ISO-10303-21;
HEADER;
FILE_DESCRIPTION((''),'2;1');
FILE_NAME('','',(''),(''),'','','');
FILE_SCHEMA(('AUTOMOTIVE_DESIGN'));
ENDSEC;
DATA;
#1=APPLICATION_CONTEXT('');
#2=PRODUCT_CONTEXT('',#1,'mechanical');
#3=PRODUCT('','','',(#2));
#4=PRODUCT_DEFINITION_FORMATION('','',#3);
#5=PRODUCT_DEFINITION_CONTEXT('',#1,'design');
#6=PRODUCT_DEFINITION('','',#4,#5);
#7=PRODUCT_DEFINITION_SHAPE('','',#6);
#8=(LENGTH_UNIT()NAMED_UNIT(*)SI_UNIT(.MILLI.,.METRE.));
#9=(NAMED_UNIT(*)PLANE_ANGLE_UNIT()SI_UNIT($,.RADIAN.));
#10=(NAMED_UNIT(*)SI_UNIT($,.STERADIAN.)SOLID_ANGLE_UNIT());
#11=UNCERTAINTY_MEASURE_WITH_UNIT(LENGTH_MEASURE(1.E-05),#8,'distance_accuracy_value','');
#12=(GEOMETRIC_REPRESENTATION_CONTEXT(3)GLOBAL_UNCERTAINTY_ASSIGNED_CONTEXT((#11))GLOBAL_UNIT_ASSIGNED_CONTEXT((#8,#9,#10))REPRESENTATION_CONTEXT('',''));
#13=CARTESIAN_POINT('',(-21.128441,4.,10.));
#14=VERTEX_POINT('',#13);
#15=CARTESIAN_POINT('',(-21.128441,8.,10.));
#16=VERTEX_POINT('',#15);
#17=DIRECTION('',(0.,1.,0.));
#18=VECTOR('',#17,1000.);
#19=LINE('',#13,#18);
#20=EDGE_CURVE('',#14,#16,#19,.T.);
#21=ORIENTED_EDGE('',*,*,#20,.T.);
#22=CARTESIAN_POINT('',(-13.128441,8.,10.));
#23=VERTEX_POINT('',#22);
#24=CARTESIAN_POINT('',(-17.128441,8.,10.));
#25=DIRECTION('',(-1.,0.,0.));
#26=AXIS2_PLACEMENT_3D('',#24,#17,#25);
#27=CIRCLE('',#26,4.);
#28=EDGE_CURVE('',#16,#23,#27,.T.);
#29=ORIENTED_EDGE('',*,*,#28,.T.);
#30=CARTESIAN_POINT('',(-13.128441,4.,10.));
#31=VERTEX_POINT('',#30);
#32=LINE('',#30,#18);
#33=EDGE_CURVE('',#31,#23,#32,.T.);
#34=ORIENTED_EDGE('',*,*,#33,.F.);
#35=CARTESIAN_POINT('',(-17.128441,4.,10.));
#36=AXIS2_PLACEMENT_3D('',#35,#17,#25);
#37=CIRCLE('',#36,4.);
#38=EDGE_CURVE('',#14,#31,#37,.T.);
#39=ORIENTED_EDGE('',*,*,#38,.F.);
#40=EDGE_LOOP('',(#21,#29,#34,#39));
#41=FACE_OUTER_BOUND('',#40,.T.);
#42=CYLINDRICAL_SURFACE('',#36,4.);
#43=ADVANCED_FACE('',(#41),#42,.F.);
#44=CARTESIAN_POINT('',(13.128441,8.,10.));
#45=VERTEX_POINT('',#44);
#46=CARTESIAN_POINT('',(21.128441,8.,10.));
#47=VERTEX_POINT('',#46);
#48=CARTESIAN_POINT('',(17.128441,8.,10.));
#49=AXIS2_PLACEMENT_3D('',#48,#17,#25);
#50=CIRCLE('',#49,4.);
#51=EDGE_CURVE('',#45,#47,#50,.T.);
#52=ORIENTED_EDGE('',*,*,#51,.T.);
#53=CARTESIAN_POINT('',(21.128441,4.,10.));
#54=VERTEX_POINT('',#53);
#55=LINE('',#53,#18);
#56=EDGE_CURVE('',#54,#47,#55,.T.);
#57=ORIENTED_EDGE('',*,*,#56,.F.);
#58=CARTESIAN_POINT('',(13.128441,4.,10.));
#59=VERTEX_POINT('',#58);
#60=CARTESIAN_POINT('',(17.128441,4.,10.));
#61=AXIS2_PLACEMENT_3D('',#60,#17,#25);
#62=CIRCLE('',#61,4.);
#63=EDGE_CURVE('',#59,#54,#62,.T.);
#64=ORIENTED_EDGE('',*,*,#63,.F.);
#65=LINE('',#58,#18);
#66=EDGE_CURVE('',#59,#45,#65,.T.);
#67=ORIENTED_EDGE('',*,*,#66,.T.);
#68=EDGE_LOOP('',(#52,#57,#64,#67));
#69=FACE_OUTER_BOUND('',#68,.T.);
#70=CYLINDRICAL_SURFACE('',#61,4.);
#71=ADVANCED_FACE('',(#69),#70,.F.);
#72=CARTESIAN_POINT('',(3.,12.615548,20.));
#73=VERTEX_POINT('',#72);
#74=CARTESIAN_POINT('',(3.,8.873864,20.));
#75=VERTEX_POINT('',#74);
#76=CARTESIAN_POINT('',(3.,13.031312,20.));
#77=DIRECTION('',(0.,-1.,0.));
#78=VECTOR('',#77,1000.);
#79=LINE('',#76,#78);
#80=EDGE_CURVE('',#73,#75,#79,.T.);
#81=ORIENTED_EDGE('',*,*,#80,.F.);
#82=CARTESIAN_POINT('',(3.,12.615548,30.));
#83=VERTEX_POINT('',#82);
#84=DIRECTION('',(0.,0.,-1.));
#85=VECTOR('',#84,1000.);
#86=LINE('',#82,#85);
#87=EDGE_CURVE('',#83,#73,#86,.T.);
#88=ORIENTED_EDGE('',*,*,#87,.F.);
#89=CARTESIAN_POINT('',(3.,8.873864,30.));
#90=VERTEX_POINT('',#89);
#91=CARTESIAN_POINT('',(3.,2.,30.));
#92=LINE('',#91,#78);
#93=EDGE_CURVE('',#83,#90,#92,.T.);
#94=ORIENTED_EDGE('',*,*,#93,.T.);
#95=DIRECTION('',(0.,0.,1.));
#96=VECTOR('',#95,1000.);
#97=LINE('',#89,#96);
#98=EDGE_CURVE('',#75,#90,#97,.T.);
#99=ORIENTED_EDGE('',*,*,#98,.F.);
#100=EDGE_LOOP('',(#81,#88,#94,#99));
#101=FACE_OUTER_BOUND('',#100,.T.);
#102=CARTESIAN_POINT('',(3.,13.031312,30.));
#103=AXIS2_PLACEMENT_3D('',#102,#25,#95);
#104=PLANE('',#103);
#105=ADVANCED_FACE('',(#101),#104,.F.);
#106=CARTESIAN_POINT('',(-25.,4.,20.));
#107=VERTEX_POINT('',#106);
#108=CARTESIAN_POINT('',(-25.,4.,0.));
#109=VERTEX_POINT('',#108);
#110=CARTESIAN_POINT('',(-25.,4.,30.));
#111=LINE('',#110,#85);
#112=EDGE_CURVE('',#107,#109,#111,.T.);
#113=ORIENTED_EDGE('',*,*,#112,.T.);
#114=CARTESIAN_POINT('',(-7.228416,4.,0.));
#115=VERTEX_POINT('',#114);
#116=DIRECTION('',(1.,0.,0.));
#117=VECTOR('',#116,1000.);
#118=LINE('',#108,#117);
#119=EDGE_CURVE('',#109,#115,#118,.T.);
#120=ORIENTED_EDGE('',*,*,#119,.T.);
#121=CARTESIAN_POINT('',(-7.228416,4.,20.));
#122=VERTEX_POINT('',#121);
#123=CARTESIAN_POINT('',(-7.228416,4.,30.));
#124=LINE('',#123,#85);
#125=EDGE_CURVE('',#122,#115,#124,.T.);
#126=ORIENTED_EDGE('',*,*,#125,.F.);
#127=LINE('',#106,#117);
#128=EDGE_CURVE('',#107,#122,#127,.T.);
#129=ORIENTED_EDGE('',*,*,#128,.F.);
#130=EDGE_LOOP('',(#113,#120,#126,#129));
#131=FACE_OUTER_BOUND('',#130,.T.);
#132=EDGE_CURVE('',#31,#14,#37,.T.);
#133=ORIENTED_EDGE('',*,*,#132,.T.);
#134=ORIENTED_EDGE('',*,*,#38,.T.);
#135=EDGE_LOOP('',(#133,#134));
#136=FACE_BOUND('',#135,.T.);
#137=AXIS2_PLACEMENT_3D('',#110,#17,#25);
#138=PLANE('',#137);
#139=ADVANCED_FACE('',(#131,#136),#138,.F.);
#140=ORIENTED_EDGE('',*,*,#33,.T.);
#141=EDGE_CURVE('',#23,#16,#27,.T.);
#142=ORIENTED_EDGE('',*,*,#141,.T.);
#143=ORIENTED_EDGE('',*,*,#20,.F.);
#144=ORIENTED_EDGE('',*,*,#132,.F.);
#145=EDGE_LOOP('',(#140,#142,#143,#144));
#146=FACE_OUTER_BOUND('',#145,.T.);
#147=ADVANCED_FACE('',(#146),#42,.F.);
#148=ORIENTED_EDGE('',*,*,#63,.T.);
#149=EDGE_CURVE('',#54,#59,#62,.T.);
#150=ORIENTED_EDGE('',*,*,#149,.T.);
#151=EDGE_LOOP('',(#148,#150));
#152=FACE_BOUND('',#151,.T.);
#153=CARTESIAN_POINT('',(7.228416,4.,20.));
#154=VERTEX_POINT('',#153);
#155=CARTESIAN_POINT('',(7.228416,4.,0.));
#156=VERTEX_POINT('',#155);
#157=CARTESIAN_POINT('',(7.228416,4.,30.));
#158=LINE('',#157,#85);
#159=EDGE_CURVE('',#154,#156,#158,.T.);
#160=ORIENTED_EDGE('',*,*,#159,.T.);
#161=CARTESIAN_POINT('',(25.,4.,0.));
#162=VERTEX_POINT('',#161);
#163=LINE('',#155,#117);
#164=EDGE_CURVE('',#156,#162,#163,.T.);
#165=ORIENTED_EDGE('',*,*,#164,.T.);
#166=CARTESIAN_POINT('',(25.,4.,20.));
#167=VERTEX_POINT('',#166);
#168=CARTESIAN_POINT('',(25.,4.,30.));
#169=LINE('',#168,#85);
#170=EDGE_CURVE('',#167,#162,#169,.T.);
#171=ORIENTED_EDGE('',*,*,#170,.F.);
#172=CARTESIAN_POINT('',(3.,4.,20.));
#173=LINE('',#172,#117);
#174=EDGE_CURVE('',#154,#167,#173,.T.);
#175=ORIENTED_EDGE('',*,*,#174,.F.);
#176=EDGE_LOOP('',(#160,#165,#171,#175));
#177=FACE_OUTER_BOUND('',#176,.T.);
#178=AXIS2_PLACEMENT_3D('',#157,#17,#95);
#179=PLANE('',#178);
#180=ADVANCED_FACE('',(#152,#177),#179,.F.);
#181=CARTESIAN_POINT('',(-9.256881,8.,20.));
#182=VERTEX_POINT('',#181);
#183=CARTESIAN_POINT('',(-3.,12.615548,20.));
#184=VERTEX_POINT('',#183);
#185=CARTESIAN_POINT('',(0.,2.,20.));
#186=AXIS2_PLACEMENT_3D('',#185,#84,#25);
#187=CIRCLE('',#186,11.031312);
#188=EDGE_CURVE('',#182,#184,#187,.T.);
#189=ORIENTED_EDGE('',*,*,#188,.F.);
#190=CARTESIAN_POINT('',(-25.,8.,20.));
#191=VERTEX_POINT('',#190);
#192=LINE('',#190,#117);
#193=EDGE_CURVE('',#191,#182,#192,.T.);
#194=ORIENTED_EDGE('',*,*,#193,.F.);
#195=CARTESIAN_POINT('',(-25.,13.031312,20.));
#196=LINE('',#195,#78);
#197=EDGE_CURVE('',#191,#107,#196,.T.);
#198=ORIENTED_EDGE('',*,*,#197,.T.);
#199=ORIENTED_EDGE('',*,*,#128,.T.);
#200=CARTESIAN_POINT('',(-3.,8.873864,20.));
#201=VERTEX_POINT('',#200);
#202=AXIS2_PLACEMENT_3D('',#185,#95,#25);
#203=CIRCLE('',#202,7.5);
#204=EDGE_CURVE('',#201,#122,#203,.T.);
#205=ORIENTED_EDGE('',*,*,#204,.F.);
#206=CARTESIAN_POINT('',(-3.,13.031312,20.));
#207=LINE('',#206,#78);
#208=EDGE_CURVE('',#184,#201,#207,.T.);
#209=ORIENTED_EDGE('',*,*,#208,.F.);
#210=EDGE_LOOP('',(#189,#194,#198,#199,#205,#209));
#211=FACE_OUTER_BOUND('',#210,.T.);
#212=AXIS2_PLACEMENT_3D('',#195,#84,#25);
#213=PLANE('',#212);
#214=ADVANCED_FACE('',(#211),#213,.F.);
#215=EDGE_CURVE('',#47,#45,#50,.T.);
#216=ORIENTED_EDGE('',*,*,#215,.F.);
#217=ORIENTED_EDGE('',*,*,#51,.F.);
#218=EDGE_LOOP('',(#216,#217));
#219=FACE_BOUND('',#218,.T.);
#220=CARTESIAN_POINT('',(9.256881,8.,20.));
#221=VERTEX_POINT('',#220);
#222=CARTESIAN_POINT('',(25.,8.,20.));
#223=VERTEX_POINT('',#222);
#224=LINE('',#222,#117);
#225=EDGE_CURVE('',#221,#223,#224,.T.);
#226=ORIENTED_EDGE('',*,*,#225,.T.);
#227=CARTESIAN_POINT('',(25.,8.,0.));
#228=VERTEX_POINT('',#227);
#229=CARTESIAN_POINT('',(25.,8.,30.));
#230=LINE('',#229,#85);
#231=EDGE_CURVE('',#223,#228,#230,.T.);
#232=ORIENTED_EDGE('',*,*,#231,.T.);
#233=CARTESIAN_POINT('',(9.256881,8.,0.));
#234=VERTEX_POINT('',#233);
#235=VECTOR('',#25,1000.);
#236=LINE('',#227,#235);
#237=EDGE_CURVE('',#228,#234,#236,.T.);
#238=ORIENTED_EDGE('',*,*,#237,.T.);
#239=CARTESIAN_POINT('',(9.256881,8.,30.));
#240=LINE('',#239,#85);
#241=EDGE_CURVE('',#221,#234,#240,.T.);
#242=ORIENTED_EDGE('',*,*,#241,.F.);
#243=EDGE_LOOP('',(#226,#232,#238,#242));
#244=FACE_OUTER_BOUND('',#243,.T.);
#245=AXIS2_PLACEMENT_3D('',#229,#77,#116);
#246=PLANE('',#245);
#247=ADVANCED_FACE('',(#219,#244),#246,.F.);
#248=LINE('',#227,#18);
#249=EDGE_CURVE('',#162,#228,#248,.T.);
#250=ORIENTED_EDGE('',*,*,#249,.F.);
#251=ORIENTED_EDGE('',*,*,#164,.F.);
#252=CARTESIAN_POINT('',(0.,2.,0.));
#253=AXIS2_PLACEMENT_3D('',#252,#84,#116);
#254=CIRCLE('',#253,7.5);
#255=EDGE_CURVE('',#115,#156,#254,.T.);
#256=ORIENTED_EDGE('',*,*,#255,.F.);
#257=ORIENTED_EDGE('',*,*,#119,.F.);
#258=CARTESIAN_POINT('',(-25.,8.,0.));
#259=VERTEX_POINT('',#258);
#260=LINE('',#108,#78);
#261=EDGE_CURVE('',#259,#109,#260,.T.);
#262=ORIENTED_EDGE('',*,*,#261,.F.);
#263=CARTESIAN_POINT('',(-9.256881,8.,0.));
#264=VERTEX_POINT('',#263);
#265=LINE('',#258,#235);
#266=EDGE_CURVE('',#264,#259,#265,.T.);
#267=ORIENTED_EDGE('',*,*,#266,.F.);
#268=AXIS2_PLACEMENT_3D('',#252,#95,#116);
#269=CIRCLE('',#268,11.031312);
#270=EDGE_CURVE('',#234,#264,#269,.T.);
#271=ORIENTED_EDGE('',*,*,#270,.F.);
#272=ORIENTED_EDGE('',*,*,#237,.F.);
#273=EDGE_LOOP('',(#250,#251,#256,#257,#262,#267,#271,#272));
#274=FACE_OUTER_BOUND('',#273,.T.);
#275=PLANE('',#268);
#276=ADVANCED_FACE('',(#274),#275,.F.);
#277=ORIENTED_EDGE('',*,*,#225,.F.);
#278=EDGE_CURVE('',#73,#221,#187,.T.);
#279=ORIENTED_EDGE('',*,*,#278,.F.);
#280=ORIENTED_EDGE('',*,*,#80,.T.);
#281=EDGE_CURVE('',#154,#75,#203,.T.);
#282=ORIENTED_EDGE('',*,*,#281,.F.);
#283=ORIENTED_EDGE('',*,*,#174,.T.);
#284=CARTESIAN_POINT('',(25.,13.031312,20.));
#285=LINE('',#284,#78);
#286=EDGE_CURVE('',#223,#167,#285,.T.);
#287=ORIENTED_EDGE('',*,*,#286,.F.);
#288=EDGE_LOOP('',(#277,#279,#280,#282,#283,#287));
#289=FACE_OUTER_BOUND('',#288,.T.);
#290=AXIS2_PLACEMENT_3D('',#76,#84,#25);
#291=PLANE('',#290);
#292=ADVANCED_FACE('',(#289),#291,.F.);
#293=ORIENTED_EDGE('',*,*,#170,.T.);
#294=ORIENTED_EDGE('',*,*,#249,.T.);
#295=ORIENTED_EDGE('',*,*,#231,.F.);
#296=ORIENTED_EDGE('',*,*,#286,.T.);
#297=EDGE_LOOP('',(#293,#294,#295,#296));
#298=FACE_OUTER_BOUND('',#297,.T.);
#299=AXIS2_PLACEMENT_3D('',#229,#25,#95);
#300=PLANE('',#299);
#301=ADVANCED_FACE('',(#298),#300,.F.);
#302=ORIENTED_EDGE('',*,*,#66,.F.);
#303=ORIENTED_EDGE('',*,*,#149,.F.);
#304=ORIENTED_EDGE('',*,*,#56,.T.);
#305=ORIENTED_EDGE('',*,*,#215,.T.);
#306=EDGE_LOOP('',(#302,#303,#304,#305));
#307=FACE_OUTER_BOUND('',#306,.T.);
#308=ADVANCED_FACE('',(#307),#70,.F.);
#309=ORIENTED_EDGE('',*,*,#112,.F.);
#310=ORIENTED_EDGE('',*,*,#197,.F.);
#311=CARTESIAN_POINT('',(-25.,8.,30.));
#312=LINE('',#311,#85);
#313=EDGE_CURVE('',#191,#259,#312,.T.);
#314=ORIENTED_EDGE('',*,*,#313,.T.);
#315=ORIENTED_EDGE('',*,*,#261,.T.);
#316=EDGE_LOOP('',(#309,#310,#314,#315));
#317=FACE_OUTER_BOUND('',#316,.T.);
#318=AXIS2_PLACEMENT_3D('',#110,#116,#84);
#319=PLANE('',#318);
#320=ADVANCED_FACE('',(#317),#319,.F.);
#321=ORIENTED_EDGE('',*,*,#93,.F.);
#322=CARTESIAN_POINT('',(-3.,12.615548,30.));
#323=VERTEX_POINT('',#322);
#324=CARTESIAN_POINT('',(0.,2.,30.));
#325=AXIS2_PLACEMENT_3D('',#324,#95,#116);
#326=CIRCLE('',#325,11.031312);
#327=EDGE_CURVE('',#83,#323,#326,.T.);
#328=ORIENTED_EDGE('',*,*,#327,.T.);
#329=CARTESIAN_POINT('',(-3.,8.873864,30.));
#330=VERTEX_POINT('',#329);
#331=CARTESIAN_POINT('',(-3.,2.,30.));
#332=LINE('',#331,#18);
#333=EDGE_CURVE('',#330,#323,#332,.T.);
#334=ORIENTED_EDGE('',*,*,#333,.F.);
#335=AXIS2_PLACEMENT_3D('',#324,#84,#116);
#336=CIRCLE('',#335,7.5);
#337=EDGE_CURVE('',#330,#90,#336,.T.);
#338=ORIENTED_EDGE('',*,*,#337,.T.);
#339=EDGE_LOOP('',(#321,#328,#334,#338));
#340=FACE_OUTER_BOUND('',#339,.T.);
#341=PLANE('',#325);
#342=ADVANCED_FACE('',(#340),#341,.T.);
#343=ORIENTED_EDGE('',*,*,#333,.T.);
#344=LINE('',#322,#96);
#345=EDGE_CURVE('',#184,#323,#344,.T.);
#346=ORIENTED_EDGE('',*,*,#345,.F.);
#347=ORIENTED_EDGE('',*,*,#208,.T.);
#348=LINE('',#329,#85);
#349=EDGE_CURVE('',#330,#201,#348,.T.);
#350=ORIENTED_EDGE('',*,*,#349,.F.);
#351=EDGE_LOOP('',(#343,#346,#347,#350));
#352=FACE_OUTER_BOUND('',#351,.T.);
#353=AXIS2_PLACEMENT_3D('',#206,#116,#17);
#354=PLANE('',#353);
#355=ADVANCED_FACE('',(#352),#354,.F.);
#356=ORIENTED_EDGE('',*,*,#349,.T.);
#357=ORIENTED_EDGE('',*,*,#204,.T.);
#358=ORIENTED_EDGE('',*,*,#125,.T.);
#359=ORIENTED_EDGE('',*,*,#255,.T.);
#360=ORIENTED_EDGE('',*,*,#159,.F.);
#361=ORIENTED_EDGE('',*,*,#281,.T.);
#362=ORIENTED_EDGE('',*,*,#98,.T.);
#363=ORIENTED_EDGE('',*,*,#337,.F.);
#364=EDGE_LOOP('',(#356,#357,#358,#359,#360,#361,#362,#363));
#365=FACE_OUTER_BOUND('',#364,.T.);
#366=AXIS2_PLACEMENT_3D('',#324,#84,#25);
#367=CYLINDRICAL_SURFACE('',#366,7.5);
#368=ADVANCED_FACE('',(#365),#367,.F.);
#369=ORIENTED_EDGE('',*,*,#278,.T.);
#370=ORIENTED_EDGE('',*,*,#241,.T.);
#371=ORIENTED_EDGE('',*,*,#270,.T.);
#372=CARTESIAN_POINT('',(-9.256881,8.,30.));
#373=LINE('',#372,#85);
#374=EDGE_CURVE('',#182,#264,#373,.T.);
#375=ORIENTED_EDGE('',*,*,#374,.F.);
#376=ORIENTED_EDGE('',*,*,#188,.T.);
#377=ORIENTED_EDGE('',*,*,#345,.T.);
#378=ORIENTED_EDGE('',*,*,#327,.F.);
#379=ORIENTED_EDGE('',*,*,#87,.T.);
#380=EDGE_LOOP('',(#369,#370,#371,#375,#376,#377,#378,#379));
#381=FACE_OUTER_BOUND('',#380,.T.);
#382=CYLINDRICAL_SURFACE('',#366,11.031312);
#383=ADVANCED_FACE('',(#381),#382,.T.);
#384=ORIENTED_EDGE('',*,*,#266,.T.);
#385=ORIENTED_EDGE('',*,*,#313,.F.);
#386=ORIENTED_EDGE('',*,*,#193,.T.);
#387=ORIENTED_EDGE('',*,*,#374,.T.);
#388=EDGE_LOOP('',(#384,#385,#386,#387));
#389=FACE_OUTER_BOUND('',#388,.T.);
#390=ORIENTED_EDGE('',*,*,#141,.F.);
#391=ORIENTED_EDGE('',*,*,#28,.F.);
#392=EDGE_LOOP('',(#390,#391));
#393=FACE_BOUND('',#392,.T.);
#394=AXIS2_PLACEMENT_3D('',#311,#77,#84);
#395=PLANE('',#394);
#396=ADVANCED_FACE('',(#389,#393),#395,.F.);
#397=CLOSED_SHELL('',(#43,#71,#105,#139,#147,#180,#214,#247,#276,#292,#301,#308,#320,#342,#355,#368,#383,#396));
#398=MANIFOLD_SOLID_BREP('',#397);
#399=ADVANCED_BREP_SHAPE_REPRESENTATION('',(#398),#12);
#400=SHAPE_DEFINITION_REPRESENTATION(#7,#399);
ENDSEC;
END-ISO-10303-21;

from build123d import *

# Parameters (mm, degrees)
EXTRUDE_5_DEPTH     = 30
SKETCH_5_W          = 22
SKETCH_5_H          = 10
CUT_EXTRUDE_7_DEPTH = 41.081973509
SKETCH_6_R          = 4
CUT_EXTRUDE_8_DEPTH = 40.374028275


with BuildPart() as part:
    # 草图1 → 拉伸5 (new body)
    with BuildSketch(Plane.XY):
        with BuildLine():
            Line((7.228416147, 4), (25, 4))
            Line((25, 4), (25, 8))
            Line((25, 8), (9.256881183, 8))
            ThreePointArc((9.256881183, 8), (0, 13.031312217), (-9.256881183, 8))
            Line((-9.256881183, 8), (-25, 8))
            Line((-25, 8), (-25, 4))
            Line((-25, 4), (-7.228416147, 4))
            ThreePointArc((-7.228416147, 4), (0, 9.5), (7.228416147, 4))
        make_face()
    extrude(amount=EXTRUDE_5_DEPTH)

    # 草图5 → 拉伸7 (cut, through all)
    with BuildSketch(Plane.XZ.offset(-4)):
        with Locations((-14, 25)):
            Rectangle(SKETCH_5_W, SKETCH_5_H)
        with Locations((14, 25)):
            Rectangle(SKETCH_5_W, SKETCH_5_H)
    extrude(amount=-CUT_EXTRUDE_7_DEPTH, mode=Mode.SUBTRACT)

    # 草图6 → 拉伸8 (cut, through all)
    with BuildSketch(Plane(origin=(0, 8, 0), x_dir=(1, 0, 0), z_dir=(0, 1, 0))):
        with Locations(Location((-17.128440592, -10, 0), (0, 0, 180))):
            Circle(SKETCH_6_R)
        with Locations(Location((17.128440592, -10, 0), (0, 0, 180))):
            Circle(SKETCH_6_R)
    extrude(amount=-CUT_EXTRUDE_8_DEPTH, mode=Mode.SUBTRACT)


solid = part.part
